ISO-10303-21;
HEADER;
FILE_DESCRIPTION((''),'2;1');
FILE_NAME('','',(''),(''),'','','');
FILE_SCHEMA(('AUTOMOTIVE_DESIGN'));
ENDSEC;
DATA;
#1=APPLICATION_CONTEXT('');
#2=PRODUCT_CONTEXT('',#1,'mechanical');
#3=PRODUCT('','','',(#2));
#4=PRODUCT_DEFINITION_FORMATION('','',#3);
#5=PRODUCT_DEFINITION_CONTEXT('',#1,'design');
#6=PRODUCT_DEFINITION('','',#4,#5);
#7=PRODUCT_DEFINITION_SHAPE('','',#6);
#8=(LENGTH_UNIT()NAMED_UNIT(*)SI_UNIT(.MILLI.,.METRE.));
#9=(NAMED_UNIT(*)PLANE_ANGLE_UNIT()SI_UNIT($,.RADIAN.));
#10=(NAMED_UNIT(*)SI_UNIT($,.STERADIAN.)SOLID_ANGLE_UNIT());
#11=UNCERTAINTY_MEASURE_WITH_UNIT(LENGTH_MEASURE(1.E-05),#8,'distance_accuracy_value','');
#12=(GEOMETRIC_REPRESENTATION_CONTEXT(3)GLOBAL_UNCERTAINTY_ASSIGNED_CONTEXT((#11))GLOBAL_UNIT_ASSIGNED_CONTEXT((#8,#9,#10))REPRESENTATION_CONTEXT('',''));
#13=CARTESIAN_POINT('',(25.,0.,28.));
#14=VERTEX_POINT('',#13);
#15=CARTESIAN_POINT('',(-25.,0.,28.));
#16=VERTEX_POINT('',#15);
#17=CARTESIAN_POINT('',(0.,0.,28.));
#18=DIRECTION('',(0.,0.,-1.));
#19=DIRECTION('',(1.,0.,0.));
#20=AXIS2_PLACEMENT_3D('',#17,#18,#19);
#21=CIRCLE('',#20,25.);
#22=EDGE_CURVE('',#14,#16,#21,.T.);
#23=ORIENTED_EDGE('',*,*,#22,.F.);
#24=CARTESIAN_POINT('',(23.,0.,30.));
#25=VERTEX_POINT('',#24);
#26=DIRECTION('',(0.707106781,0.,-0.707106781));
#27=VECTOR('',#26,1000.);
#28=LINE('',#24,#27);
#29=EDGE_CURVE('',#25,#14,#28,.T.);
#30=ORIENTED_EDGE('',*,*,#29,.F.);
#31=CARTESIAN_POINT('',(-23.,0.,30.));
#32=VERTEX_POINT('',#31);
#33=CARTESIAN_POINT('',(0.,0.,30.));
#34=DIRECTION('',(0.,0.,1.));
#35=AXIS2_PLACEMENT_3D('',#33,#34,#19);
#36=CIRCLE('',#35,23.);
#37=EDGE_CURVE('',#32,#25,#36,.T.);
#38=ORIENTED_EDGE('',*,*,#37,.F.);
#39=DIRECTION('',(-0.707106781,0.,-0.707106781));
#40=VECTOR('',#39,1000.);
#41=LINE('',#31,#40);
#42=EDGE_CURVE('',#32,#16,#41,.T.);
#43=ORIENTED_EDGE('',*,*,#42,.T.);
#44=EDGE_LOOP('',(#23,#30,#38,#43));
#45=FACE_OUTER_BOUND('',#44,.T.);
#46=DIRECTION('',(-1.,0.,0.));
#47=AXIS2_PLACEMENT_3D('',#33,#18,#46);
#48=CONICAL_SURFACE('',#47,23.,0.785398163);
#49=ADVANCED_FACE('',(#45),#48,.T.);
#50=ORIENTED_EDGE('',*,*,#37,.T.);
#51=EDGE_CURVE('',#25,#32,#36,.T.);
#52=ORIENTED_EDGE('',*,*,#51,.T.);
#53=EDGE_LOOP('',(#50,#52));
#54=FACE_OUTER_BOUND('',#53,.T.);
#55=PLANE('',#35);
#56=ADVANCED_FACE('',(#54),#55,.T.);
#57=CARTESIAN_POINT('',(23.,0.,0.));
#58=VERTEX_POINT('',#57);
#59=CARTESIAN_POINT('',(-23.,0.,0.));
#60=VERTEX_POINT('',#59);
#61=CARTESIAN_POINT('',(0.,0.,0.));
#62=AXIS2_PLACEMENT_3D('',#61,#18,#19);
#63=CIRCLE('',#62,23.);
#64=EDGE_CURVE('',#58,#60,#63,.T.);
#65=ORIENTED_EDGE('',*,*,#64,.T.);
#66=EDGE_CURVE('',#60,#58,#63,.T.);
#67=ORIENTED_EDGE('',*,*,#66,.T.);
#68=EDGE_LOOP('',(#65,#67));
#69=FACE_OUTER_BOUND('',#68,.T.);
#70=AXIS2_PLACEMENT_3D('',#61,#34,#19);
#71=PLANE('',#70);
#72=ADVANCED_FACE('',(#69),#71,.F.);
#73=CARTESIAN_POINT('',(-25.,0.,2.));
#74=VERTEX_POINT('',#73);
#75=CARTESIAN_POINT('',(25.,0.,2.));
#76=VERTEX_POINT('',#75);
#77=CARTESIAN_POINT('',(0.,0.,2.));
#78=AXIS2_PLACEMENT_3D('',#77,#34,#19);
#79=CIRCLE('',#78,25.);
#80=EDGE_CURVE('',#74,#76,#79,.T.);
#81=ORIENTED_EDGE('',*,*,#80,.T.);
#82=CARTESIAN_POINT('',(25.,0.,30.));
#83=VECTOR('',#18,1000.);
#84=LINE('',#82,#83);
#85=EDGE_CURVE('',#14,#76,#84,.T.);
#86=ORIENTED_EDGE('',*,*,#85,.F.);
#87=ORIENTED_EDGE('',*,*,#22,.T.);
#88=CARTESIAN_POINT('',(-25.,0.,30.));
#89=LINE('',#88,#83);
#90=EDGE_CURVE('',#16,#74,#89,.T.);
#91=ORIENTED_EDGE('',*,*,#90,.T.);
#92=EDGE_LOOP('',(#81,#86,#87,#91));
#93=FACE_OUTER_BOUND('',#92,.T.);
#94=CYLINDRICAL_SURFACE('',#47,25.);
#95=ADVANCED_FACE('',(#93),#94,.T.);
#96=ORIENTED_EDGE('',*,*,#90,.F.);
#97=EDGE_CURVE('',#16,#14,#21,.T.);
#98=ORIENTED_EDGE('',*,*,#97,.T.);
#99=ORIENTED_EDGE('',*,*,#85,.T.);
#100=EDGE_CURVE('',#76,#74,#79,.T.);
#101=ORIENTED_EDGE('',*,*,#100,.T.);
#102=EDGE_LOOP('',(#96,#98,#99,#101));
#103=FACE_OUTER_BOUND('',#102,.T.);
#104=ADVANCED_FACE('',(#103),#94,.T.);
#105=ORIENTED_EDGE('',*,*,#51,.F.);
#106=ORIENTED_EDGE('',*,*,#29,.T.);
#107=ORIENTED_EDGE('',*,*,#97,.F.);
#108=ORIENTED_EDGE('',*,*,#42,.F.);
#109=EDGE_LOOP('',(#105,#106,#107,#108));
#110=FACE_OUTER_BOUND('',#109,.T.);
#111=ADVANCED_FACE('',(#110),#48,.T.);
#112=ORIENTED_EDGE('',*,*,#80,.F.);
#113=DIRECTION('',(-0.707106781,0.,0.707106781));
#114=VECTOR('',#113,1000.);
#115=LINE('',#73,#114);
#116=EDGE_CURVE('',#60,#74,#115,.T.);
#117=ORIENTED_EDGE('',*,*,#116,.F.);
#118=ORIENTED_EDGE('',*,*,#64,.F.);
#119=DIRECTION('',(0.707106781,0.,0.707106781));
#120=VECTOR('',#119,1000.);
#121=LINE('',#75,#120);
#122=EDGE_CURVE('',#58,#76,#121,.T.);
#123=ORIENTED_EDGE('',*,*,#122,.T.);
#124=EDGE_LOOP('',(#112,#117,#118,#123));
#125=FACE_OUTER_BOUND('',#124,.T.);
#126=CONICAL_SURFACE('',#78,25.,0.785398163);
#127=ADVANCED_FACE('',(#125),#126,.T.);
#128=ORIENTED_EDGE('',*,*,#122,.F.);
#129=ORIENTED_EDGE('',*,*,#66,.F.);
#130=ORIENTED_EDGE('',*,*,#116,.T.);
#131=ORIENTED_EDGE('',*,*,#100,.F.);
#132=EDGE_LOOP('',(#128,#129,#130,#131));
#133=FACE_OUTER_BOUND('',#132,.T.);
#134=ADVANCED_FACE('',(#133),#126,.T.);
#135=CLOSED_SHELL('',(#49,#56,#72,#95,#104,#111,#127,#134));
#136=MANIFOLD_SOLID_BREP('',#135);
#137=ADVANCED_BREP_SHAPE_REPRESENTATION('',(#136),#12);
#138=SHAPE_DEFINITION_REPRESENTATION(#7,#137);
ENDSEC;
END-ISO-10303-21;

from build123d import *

# Parameters (mm, degrees)
SKETCH1_R           = 25
BOSS_EXTRUDE1_DEPTH = 30
CHAMFER1_SIZE       = 2


with BuildPart() as part:
    # Sketch1 → Boss-Extrude1 (new body)
    with BuildSketch(Plane.XY):
        Circle(SKETCH1_R)
    extrude(amount=BOSS_EXTRUDE1_DEPTH)

    # Chamfer1
    chamfer1_edges = [part.edges().sort_by_distance(p)[0] for p in [
        (-25, 0, 0),
        (-25, 0, 30),
    ]]
    chamfer(chamfer1_edges, length=CHAMFER1_SIZE)


solid = part.part
